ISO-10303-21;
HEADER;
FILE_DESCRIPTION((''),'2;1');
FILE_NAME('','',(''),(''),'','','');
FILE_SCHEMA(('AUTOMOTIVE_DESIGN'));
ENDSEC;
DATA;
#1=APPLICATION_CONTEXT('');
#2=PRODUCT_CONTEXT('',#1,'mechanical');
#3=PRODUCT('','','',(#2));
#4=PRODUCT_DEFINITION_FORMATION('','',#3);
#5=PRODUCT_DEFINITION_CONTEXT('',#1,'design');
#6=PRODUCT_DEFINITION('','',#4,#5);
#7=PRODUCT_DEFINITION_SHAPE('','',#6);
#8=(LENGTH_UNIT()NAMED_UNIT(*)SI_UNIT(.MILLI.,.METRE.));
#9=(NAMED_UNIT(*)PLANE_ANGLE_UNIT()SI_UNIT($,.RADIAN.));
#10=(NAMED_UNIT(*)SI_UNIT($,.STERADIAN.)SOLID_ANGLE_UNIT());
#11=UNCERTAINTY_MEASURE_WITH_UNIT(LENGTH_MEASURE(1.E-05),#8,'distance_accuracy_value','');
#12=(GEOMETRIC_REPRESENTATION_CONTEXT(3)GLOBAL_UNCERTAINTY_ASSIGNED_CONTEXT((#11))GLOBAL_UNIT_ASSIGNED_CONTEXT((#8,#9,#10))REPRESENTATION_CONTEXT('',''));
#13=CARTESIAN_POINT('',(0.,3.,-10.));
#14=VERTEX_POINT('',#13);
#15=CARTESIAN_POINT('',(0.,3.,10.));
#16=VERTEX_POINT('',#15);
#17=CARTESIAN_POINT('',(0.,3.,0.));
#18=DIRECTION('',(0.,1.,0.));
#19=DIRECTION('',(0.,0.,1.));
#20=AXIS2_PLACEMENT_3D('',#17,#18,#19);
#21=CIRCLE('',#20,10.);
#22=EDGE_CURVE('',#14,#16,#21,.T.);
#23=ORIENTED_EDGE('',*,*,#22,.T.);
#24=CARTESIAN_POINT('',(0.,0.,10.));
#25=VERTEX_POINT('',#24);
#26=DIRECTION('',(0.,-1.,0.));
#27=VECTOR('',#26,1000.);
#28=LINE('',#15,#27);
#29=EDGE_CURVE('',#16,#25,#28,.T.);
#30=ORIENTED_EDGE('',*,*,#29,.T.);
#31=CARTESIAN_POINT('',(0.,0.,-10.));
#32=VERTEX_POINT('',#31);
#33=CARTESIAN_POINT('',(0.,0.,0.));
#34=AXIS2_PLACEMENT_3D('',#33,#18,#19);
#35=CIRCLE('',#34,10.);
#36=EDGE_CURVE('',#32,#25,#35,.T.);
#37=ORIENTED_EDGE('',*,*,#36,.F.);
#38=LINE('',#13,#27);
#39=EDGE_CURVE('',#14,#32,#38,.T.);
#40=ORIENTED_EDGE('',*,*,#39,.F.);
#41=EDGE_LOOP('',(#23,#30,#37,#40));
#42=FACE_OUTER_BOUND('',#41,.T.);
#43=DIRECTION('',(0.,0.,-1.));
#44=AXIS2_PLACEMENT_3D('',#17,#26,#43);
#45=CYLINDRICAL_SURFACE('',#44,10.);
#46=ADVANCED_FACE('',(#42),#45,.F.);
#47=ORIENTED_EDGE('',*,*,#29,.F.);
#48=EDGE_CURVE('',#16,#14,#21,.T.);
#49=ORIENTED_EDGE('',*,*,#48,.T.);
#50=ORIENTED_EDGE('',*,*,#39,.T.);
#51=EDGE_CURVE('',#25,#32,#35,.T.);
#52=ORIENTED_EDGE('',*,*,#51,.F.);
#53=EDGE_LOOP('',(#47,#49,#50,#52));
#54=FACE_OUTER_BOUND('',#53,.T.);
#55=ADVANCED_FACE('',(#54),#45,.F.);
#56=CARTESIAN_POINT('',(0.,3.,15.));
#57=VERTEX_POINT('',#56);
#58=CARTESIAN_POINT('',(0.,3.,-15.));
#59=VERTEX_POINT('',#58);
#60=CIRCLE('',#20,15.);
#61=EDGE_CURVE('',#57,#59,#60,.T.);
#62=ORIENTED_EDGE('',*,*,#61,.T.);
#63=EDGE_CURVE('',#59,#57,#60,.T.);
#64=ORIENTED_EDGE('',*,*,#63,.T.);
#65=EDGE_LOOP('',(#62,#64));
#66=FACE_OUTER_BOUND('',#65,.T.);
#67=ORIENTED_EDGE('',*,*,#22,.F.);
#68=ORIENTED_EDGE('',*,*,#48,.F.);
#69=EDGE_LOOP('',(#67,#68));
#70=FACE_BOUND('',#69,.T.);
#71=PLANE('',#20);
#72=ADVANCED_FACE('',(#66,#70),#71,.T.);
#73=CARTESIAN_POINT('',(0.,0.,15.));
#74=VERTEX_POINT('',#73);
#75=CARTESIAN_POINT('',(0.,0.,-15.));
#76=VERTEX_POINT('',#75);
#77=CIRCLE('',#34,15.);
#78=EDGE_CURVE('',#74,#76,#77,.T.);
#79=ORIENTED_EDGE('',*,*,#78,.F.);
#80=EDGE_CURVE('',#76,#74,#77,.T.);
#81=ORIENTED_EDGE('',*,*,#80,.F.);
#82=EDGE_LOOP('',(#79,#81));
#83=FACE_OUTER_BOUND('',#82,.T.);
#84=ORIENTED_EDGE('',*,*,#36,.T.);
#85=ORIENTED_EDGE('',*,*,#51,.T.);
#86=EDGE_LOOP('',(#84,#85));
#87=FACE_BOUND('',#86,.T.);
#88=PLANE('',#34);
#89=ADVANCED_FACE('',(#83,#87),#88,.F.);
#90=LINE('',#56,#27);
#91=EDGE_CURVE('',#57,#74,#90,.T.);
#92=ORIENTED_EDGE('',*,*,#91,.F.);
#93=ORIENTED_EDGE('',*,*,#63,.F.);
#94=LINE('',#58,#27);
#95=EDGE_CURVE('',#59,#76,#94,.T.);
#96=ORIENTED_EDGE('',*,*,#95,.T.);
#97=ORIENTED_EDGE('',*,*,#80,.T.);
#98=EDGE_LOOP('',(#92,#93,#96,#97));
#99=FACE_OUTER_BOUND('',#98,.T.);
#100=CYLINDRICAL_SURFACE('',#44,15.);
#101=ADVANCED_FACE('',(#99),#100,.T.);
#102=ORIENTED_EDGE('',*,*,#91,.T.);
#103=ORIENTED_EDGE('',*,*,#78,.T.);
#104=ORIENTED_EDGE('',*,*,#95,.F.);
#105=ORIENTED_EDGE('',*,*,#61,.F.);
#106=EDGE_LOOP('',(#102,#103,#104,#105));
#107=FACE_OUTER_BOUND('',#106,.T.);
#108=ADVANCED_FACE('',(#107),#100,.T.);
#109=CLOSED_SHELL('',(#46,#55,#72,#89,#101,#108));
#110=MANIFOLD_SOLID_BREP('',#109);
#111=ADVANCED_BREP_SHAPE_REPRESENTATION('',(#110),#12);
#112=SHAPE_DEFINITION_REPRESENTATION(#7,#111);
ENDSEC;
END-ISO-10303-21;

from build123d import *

# Parameters (mm, degrees)
SKETCH1_R           = 15
SKETCH1_R_2         = 10
BOSS_EXTRUDE1_DEPTH = 3


with BuildPart() as part:
    # Sketch1 → Boss-Extrude1 (new body)
    with BuildSketch(Plane(origin=(0, 0, 0), x_dir=(1, 0, 0), z_dir=(0, 1, 0))):
        with Locations(Location((0, 0, 0), (0, 0, 270))):
            Circle(SKETCH1_R)
        with Locations(Location((0, 0, 0), (0, 0, 270))):
            Circle(SKETCH1_R_2, mode=Mode.SUBTRACT)
    extrude(amount=BOSS_EXTRUDE1_DEPTH)


solid = part.part
